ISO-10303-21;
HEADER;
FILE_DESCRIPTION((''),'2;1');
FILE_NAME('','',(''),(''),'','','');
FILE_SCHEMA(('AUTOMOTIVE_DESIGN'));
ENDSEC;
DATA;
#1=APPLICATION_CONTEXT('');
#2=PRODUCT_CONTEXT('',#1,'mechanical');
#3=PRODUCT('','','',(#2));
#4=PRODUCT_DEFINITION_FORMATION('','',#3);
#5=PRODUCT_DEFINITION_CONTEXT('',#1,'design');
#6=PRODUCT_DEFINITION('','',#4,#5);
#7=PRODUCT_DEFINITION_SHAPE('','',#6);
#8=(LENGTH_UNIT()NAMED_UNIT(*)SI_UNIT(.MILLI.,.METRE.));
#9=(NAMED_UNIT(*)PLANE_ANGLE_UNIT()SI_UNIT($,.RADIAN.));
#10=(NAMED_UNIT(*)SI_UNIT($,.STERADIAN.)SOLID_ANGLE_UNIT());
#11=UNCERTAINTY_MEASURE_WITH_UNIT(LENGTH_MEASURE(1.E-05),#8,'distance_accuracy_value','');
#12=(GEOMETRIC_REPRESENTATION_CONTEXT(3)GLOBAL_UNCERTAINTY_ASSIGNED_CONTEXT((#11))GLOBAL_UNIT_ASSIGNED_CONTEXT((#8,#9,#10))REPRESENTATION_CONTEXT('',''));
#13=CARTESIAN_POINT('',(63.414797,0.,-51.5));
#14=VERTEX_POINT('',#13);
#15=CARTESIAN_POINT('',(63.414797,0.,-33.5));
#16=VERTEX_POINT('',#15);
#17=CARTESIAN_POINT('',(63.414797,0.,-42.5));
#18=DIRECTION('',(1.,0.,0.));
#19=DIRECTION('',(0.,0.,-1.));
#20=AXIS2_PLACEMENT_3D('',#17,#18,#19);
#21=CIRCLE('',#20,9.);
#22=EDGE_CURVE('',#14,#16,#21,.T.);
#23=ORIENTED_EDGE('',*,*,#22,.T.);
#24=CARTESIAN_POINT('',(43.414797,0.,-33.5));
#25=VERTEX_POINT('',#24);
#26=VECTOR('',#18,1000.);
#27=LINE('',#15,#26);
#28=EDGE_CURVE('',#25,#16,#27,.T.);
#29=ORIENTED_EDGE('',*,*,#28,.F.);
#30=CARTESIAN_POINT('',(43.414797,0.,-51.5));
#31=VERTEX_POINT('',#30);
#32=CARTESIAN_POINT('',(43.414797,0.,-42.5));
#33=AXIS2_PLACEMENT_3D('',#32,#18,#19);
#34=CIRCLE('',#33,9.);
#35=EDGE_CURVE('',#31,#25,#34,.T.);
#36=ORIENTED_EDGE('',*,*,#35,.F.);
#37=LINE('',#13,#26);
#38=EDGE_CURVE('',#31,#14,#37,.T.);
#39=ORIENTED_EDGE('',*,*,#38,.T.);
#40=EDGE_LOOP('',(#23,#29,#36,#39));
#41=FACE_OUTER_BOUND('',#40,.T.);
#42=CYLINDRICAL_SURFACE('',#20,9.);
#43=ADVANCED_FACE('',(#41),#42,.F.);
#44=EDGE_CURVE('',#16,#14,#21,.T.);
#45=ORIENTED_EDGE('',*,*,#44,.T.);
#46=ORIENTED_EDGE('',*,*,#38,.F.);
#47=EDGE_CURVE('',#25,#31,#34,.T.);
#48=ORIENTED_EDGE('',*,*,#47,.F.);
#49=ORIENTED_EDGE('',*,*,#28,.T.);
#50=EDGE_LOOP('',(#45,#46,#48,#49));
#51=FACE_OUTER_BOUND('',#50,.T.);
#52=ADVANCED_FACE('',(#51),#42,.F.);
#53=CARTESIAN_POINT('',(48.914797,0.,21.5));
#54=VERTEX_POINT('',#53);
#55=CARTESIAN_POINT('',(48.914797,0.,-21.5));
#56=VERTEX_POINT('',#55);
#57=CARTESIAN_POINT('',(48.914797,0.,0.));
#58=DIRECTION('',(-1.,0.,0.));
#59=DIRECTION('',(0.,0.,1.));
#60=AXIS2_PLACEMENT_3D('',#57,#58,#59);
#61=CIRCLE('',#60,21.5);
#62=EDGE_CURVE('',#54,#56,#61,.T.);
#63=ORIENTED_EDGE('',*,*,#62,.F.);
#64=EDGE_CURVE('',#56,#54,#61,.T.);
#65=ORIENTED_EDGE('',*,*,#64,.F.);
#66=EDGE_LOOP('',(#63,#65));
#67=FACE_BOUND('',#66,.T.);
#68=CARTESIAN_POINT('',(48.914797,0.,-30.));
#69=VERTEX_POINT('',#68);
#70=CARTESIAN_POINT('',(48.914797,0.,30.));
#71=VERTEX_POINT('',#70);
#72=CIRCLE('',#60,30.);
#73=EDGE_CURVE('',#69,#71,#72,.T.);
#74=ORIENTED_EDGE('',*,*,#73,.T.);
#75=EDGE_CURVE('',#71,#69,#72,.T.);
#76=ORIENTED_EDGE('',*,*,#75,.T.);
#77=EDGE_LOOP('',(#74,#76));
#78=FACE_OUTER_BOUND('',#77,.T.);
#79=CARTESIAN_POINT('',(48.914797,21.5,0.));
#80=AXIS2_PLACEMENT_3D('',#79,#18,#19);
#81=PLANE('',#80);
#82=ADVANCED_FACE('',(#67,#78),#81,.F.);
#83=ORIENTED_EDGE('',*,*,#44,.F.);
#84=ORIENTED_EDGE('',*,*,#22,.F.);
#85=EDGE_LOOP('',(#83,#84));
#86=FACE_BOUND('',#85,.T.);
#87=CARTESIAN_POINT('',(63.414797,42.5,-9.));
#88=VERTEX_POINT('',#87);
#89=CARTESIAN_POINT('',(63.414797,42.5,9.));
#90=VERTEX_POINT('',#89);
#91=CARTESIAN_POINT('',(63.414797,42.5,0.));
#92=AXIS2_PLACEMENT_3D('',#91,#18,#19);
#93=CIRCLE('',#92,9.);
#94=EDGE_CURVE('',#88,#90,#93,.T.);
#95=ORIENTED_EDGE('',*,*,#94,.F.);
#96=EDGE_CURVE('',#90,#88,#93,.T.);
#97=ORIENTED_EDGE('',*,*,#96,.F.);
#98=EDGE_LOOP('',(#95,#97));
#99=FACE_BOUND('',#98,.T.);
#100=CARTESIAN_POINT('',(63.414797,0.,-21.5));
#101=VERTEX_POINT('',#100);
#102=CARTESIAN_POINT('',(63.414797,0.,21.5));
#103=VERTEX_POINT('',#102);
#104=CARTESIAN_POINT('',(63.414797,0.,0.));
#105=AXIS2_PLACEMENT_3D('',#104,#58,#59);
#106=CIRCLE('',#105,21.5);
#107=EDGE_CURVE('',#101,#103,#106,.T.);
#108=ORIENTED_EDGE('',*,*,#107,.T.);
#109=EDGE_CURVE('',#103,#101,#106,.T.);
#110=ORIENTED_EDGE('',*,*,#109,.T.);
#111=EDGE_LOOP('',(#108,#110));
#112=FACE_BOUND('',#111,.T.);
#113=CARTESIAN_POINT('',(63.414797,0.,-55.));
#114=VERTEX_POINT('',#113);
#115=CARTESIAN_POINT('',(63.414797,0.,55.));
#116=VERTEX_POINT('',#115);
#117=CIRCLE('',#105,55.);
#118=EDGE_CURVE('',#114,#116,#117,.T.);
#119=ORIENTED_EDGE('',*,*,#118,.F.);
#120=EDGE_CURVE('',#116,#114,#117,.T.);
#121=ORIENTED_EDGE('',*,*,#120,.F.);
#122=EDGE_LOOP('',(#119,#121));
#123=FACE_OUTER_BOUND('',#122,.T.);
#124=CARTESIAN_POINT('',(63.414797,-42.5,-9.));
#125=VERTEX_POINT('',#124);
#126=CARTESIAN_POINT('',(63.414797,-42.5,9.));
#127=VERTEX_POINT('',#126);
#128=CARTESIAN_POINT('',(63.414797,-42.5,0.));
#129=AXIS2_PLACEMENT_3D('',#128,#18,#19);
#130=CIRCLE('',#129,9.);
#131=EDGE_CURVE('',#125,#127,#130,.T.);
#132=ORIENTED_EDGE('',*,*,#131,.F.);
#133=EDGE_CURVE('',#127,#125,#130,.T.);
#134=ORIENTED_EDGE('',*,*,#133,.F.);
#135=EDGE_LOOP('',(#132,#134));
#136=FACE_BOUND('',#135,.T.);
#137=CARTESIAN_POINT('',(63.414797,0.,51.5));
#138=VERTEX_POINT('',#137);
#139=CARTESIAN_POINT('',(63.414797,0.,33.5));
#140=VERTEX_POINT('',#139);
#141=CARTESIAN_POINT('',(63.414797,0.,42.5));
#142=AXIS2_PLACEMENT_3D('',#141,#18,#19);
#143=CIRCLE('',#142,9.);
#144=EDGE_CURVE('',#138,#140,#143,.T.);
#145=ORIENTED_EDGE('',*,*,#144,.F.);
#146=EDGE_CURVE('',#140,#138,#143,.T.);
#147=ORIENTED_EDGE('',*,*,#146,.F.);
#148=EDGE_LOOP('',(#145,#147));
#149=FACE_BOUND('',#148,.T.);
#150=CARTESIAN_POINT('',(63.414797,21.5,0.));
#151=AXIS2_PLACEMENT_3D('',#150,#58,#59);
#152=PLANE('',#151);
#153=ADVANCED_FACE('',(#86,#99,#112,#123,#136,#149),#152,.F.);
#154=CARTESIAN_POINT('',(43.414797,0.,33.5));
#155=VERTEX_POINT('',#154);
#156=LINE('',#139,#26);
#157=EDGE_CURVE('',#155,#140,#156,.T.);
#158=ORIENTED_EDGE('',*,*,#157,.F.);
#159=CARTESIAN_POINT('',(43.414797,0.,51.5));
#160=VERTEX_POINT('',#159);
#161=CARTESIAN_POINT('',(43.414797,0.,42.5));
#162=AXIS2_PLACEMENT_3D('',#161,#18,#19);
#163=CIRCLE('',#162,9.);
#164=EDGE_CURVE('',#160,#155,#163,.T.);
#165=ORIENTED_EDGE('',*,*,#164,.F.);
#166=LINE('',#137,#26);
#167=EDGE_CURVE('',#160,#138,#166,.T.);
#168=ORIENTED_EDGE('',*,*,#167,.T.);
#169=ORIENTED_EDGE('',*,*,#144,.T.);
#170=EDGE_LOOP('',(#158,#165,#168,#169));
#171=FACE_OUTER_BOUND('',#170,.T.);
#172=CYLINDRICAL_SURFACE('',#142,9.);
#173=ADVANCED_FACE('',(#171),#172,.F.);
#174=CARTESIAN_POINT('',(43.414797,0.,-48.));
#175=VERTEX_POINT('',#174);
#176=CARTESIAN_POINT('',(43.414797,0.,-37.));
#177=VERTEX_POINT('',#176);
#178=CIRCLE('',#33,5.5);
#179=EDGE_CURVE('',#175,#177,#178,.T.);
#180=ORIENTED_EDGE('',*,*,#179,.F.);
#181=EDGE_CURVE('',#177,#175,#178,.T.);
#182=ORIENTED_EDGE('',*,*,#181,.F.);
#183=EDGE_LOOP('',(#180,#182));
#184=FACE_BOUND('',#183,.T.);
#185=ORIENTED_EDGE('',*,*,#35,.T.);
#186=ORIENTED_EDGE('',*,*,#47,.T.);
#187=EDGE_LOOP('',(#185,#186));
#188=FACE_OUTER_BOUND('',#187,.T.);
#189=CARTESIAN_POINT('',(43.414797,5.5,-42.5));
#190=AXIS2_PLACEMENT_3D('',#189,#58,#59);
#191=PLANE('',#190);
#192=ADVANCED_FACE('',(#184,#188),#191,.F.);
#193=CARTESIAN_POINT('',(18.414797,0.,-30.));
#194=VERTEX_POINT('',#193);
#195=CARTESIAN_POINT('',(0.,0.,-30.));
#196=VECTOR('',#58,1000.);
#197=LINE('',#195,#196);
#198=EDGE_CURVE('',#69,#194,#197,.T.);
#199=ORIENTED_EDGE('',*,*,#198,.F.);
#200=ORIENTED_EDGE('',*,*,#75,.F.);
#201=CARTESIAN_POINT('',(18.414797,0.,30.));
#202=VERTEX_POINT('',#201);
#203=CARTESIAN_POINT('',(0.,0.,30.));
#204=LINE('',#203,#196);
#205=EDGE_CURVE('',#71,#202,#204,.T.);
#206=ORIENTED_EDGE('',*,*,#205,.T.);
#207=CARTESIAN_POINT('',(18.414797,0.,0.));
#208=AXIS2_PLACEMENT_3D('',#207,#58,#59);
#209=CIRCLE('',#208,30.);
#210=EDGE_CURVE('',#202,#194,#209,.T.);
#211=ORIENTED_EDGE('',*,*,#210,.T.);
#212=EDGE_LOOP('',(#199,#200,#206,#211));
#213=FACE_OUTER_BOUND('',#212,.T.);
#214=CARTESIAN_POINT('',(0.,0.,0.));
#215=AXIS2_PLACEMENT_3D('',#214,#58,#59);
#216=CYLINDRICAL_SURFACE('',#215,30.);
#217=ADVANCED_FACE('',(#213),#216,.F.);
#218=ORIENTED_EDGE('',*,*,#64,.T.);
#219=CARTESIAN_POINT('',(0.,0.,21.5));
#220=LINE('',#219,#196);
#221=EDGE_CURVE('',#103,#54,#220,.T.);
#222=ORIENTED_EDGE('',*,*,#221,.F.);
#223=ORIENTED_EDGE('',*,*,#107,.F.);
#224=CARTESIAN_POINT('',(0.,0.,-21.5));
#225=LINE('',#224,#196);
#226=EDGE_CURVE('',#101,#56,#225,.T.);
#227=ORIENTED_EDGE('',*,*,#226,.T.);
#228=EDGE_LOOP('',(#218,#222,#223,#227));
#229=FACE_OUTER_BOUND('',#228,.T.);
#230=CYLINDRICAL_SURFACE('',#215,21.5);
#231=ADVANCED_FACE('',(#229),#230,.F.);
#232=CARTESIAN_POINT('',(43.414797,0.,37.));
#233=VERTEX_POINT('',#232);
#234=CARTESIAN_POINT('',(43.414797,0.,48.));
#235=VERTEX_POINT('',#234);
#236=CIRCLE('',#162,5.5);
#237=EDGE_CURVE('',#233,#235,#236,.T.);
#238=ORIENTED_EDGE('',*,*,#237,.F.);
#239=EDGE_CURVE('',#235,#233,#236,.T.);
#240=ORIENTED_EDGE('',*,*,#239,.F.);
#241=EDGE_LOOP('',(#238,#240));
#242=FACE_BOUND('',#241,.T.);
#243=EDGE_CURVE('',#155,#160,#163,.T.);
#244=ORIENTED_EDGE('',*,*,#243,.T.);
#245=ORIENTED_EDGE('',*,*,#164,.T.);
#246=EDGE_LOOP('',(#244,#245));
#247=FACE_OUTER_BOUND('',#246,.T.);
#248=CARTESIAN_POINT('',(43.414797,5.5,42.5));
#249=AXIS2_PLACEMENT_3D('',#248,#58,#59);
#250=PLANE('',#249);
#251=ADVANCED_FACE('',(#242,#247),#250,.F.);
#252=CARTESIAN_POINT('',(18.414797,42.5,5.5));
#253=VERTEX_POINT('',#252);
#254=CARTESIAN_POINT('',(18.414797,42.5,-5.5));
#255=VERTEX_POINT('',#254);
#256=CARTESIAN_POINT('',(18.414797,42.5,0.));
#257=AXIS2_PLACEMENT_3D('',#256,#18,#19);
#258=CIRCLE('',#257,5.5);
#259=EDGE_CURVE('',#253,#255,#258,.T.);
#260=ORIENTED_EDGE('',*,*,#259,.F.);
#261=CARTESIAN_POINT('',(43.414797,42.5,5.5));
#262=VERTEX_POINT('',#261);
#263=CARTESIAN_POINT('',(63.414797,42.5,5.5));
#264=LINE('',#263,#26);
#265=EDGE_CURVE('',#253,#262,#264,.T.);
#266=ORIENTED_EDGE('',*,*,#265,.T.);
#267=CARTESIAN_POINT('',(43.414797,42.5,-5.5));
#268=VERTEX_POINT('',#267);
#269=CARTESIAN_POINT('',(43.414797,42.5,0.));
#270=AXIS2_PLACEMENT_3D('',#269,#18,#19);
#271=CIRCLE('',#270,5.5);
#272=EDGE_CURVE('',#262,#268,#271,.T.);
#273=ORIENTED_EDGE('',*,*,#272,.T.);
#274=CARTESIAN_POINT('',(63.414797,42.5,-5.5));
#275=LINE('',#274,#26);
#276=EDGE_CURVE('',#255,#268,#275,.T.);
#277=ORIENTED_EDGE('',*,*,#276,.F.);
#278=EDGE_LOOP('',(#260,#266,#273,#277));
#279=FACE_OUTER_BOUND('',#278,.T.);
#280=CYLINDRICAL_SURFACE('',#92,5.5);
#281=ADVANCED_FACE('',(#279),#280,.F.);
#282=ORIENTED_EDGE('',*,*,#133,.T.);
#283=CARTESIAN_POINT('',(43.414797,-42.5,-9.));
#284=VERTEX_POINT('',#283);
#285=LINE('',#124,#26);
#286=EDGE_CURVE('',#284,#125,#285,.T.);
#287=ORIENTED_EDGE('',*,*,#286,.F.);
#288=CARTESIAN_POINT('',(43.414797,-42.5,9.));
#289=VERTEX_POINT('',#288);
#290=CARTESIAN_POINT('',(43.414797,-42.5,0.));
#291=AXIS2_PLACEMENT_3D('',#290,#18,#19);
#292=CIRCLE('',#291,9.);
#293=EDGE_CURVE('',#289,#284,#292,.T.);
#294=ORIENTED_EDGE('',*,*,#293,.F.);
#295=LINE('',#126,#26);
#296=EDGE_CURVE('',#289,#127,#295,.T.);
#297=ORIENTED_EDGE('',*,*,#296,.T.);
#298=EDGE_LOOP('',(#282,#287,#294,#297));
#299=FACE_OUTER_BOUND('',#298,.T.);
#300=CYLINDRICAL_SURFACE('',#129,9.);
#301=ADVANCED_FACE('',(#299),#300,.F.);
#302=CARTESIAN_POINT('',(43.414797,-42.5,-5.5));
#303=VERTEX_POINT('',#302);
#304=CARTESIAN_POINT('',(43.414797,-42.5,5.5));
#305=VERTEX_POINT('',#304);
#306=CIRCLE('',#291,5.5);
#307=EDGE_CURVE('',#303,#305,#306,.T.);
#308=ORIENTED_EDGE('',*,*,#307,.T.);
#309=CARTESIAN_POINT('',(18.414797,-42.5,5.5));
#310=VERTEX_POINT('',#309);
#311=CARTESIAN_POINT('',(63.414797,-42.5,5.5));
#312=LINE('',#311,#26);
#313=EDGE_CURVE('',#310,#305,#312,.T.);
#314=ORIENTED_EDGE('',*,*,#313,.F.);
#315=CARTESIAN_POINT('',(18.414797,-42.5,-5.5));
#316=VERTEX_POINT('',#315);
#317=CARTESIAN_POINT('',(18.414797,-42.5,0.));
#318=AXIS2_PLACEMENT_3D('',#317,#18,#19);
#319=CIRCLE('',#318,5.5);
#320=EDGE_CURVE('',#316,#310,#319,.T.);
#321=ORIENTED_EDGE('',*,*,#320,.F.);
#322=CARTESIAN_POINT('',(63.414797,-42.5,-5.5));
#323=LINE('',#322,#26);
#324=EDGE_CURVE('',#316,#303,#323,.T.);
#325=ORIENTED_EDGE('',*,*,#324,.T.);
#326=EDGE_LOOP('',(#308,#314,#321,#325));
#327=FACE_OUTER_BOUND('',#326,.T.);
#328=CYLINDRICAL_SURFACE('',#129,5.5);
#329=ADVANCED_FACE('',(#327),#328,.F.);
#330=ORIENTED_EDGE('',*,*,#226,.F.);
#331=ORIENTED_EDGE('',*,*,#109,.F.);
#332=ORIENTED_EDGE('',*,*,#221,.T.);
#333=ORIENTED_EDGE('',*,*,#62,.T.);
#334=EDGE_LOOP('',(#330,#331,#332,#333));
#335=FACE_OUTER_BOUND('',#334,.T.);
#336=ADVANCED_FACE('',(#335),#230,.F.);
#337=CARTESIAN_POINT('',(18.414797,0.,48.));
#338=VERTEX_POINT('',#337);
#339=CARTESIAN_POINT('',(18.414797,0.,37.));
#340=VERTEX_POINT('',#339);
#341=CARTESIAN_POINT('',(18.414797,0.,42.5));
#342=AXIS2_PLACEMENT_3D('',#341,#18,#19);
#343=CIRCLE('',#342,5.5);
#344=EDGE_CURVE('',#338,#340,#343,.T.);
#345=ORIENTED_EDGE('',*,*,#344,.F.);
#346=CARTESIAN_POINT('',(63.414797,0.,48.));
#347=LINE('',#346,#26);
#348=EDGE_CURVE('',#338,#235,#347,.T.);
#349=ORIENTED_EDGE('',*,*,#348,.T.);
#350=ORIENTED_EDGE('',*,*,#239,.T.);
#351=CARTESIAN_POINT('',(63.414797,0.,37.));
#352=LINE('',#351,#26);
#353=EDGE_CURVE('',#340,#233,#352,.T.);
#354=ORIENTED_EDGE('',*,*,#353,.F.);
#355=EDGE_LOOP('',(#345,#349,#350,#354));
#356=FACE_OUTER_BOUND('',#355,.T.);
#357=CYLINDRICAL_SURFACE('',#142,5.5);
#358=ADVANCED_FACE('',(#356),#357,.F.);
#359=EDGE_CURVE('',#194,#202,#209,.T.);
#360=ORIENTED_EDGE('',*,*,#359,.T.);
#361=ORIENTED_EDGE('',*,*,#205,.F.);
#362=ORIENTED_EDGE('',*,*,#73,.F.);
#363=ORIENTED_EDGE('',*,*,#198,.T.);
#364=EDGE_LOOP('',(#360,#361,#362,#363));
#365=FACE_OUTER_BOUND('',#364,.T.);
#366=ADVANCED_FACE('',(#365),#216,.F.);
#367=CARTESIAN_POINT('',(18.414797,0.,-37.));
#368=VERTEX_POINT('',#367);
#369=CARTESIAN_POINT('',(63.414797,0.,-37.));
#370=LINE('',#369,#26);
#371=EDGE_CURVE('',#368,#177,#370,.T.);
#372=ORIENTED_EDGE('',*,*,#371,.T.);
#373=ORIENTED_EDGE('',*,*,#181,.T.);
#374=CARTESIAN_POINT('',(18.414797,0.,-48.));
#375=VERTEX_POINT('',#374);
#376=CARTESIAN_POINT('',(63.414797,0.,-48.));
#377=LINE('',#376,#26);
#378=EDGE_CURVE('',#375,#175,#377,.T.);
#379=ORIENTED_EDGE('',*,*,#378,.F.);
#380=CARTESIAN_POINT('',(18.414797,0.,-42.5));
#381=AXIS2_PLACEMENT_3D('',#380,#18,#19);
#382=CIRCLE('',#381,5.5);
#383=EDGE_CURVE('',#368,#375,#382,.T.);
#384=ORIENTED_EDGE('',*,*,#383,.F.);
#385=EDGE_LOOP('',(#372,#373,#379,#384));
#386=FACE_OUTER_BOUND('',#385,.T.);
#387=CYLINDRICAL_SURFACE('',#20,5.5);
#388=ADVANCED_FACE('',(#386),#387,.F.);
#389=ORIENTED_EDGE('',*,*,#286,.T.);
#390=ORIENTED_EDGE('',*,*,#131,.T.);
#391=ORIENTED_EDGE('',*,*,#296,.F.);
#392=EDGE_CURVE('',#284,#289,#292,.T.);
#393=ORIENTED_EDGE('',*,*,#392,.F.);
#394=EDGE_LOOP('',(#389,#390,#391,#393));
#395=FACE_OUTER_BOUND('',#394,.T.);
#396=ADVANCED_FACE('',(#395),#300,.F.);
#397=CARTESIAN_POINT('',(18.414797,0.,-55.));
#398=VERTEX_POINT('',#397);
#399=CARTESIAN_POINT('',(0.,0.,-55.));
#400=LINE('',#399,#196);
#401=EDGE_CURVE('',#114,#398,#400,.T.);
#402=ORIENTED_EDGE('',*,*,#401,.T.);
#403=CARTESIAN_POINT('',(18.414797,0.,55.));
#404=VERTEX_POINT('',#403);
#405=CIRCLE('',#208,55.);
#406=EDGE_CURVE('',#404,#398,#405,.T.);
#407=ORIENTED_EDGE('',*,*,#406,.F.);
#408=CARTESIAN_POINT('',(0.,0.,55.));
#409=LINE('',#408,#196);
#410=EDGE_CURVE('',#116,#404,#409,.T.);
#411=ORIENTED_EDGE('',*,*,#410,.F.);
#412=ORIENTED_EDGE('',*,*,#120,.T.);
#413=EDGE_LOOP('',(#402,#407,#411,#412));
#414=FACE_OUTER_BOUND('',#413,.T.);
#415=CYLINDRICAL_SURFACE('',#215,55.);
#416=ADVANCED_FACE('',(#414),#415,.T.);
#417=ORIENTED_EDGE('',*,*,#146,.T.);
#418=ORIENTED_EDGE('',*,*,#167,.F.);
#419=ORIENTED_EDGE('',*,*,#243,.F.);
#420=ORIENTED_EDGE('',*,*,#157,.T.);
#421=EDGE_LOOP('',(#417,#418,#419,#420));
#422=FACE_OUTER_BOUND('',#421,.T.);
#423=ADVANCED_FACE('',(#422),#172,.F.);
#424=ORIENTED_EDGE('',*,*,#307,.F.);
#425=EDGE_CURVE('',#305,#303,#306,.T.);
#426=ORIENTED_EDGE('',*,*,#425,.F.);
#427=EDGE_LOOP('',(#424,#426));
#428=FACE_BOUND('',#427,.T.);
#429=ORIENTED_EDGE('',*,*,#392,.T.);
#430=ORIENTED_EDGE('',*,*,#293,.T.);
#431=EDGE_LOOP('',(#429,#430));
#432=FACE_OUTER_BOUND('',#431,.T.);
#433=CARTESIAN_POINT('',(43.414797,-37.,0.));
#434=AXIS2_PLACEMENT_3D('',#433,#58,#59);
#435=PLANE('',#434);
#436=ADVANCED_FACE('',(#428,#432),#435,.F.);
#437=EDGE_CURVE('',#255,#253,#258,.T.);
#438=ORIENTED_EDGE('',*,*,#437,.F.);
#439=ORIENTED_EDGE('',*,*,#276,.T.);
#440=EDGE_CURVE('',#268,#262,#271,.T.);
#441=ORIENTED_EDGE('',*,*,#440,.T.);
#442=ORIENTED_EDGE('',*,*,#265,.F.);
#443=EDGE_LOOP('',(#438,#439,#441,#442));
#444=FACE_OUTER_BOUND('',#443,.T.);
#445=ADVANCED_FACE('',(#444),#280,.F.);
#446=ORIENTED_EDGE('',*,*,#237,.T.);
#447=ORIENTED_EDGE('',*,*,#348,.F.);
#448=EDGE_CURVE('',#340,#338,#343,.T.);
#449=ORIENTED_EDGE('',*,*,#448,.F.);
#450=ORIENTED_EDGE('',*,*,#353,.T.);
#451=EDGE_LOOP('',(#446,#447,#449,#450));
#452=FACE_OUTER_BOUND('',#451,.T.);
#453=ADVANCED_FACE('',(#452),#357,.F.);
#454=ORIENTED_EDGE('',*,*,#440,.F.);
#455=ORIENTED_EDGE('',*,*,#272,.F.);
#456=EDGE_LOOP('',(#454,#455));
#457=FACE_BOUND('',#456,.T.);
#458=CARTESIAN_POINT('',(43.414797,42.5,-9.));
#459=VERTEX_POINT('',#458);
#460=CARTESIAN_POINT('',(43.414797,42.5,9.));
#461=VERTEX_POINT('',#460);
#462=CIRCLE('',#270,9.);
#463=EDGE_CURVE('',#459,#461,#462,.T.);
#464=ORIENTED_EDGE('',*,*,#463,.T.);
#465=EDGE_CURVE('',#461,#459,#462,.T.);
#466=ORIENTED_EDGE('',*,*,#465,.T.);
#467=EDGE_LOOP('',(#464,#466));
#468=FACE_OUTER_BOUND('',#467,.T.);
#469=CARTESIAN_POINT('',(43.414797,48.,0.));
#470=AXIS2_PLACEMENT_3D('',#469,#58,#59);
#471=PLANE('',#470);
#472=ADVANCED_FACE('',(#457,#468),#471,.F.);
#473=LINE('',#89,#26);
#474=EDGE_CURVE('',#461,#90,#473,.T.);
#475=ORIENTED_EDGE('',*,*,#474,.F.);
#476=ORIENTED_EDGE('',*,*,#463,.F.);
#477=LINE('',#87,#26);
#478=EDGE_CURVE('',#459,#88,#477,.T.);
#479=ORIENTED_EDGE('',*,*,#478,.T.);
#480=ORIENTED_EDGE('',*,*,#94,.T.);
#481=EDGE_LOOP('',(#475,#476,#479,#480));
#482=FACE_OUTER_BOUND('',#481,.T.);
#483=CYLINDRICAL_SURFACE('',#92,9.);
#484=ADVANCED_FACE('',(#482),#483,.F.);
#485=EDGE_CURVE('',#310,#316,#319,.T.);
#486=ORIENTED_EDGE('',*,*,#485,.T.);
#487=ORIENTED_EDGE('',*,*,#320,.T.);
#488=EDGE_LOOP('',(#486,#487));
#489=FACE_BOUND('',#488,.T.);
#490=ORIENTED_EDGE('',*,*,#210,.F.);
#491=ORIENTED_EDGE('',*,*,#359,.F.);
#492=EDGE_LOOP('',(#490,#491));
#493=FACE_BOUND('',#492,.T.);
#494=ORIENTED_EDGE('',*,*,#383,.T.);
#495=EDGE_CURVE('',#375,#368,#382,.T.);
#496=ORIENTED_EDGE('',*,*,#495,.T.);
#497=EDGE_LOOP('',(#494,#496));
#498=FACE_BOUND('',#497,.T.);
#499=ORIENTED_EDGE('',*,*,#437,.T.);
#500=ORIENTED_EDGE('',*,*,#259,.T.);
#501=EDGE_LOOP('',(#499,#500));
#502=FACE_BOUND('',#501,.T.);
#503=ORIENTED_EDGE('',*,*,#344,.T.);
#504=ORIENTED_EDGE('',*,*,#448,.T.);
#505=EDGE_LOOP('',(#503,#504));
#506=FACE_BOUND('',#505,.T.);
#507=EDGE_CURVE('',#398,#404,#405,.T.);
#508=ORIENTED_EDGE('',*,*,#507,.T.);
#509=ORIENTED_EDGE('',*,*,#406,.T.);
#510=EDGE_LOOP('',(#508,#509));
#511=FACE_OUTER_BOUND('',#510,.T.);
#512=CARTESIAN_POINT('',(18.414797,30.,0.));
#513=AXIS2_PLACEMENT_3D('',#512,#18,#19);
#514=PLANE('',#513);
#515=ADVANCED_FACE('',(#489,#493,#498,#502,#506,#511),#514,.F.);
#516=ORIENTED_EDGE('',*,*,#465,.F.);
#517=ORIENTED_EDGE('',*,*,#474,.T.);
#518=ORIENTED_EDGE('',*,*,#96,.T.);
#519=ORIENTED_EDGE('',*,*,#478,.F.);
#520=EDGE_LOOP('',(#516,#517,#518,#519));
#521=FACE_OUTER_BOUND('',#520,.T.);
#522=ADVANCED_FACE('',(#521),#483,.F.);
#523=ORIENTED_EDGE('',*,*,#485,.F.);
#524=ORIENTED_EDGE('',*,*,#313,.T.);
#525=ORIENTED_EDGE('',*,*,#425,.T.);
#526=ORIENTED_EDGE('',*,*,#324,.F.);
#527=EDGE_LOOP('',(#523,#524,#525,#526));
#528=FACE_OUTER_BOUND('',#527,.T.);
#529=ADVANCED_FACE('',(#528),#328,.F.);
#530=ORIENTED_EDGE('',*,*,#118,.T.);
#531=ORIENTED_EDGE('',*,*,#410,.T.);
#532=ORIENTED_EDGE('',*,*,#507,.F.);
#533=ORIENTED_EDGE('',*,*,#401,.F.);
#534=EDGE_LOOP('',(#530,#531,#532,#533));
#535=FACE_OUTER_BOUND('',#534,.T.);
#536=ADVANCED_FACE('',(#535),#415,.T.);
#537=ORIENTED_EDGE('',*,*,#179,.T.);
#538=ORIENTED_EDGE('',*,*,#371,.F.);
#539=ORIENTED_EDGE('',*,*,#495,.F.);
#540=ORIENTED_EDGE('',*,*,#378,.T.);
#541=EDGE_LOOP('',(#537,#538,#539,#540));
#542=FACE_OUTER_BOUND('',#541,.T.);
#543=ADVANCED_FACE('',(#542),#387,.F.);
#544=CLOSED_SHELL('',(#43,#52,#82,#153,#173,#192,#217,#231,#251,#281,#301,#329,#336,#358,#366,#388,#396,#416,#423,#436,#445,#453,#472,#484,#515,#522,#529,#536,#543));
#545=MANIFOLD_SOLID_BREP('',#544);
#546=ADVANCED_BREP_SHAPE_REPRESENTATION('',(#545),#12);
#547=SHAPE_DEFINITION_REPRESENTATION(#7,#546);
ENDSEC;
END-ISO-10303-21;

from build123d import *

# Parameters (mm, degrees)
HOLE_SIZE_PER_SOCKET_HEAD_CAP_SCREW_TYPE_D           = 11
HOLE_SIZE_PER_SOCKET_HEAD_CAP_SCREW_TYPE_CBORE_D     = 18
HOLE_SIZE_PER_SOCKET_HEAD_CAP_SCREW_TYPE_CBORE_DEPTH = 20


with BuildPart() as part:
    # Sketch1 → Revolve1 (revolve)
    with BuildSketch(Plane.XY, mode=Mode.PRIVATE) as revolve1_sk:
        Polygon((48.914797255, 21.5), (63.414797255, 21.5), (63.414797255, 55), (18.414797255, 55), (18.414797255, 30), (48.914797255, 30), align=None)
    revolve(revolve1_sk.sketch.rotate(Axis((0, 0, 0), (1, 0, 0)), 90), axis=Axis((0, 0, 0), (1, 0, 0)))

    # Hole size per socket head cap screw type1 (through all)
    with Locations(Plane(origin=(63.414797255, 0, 0), x_dir=(0, 0, -1), z_dir=(1, 0, 0))):
        with Locations((0, 42.5), (0, -42.5), (-42.5, 0), (42.5, 0)):
            CounterBoreHole(HOLE_SIZE_PER_SOCKET_HEAD_CAP_SCREW_TYPE_D / 2, HOLE_SIZE_PER_SOCKET_HEAD_CAP_SCREW_TYPE_CBORE_D / 2, HOLE_SIZE_PER_SOCKET_HEAD_CAP_SCREW_TYPE_CBORE_DEPTH)


solid = part.part
